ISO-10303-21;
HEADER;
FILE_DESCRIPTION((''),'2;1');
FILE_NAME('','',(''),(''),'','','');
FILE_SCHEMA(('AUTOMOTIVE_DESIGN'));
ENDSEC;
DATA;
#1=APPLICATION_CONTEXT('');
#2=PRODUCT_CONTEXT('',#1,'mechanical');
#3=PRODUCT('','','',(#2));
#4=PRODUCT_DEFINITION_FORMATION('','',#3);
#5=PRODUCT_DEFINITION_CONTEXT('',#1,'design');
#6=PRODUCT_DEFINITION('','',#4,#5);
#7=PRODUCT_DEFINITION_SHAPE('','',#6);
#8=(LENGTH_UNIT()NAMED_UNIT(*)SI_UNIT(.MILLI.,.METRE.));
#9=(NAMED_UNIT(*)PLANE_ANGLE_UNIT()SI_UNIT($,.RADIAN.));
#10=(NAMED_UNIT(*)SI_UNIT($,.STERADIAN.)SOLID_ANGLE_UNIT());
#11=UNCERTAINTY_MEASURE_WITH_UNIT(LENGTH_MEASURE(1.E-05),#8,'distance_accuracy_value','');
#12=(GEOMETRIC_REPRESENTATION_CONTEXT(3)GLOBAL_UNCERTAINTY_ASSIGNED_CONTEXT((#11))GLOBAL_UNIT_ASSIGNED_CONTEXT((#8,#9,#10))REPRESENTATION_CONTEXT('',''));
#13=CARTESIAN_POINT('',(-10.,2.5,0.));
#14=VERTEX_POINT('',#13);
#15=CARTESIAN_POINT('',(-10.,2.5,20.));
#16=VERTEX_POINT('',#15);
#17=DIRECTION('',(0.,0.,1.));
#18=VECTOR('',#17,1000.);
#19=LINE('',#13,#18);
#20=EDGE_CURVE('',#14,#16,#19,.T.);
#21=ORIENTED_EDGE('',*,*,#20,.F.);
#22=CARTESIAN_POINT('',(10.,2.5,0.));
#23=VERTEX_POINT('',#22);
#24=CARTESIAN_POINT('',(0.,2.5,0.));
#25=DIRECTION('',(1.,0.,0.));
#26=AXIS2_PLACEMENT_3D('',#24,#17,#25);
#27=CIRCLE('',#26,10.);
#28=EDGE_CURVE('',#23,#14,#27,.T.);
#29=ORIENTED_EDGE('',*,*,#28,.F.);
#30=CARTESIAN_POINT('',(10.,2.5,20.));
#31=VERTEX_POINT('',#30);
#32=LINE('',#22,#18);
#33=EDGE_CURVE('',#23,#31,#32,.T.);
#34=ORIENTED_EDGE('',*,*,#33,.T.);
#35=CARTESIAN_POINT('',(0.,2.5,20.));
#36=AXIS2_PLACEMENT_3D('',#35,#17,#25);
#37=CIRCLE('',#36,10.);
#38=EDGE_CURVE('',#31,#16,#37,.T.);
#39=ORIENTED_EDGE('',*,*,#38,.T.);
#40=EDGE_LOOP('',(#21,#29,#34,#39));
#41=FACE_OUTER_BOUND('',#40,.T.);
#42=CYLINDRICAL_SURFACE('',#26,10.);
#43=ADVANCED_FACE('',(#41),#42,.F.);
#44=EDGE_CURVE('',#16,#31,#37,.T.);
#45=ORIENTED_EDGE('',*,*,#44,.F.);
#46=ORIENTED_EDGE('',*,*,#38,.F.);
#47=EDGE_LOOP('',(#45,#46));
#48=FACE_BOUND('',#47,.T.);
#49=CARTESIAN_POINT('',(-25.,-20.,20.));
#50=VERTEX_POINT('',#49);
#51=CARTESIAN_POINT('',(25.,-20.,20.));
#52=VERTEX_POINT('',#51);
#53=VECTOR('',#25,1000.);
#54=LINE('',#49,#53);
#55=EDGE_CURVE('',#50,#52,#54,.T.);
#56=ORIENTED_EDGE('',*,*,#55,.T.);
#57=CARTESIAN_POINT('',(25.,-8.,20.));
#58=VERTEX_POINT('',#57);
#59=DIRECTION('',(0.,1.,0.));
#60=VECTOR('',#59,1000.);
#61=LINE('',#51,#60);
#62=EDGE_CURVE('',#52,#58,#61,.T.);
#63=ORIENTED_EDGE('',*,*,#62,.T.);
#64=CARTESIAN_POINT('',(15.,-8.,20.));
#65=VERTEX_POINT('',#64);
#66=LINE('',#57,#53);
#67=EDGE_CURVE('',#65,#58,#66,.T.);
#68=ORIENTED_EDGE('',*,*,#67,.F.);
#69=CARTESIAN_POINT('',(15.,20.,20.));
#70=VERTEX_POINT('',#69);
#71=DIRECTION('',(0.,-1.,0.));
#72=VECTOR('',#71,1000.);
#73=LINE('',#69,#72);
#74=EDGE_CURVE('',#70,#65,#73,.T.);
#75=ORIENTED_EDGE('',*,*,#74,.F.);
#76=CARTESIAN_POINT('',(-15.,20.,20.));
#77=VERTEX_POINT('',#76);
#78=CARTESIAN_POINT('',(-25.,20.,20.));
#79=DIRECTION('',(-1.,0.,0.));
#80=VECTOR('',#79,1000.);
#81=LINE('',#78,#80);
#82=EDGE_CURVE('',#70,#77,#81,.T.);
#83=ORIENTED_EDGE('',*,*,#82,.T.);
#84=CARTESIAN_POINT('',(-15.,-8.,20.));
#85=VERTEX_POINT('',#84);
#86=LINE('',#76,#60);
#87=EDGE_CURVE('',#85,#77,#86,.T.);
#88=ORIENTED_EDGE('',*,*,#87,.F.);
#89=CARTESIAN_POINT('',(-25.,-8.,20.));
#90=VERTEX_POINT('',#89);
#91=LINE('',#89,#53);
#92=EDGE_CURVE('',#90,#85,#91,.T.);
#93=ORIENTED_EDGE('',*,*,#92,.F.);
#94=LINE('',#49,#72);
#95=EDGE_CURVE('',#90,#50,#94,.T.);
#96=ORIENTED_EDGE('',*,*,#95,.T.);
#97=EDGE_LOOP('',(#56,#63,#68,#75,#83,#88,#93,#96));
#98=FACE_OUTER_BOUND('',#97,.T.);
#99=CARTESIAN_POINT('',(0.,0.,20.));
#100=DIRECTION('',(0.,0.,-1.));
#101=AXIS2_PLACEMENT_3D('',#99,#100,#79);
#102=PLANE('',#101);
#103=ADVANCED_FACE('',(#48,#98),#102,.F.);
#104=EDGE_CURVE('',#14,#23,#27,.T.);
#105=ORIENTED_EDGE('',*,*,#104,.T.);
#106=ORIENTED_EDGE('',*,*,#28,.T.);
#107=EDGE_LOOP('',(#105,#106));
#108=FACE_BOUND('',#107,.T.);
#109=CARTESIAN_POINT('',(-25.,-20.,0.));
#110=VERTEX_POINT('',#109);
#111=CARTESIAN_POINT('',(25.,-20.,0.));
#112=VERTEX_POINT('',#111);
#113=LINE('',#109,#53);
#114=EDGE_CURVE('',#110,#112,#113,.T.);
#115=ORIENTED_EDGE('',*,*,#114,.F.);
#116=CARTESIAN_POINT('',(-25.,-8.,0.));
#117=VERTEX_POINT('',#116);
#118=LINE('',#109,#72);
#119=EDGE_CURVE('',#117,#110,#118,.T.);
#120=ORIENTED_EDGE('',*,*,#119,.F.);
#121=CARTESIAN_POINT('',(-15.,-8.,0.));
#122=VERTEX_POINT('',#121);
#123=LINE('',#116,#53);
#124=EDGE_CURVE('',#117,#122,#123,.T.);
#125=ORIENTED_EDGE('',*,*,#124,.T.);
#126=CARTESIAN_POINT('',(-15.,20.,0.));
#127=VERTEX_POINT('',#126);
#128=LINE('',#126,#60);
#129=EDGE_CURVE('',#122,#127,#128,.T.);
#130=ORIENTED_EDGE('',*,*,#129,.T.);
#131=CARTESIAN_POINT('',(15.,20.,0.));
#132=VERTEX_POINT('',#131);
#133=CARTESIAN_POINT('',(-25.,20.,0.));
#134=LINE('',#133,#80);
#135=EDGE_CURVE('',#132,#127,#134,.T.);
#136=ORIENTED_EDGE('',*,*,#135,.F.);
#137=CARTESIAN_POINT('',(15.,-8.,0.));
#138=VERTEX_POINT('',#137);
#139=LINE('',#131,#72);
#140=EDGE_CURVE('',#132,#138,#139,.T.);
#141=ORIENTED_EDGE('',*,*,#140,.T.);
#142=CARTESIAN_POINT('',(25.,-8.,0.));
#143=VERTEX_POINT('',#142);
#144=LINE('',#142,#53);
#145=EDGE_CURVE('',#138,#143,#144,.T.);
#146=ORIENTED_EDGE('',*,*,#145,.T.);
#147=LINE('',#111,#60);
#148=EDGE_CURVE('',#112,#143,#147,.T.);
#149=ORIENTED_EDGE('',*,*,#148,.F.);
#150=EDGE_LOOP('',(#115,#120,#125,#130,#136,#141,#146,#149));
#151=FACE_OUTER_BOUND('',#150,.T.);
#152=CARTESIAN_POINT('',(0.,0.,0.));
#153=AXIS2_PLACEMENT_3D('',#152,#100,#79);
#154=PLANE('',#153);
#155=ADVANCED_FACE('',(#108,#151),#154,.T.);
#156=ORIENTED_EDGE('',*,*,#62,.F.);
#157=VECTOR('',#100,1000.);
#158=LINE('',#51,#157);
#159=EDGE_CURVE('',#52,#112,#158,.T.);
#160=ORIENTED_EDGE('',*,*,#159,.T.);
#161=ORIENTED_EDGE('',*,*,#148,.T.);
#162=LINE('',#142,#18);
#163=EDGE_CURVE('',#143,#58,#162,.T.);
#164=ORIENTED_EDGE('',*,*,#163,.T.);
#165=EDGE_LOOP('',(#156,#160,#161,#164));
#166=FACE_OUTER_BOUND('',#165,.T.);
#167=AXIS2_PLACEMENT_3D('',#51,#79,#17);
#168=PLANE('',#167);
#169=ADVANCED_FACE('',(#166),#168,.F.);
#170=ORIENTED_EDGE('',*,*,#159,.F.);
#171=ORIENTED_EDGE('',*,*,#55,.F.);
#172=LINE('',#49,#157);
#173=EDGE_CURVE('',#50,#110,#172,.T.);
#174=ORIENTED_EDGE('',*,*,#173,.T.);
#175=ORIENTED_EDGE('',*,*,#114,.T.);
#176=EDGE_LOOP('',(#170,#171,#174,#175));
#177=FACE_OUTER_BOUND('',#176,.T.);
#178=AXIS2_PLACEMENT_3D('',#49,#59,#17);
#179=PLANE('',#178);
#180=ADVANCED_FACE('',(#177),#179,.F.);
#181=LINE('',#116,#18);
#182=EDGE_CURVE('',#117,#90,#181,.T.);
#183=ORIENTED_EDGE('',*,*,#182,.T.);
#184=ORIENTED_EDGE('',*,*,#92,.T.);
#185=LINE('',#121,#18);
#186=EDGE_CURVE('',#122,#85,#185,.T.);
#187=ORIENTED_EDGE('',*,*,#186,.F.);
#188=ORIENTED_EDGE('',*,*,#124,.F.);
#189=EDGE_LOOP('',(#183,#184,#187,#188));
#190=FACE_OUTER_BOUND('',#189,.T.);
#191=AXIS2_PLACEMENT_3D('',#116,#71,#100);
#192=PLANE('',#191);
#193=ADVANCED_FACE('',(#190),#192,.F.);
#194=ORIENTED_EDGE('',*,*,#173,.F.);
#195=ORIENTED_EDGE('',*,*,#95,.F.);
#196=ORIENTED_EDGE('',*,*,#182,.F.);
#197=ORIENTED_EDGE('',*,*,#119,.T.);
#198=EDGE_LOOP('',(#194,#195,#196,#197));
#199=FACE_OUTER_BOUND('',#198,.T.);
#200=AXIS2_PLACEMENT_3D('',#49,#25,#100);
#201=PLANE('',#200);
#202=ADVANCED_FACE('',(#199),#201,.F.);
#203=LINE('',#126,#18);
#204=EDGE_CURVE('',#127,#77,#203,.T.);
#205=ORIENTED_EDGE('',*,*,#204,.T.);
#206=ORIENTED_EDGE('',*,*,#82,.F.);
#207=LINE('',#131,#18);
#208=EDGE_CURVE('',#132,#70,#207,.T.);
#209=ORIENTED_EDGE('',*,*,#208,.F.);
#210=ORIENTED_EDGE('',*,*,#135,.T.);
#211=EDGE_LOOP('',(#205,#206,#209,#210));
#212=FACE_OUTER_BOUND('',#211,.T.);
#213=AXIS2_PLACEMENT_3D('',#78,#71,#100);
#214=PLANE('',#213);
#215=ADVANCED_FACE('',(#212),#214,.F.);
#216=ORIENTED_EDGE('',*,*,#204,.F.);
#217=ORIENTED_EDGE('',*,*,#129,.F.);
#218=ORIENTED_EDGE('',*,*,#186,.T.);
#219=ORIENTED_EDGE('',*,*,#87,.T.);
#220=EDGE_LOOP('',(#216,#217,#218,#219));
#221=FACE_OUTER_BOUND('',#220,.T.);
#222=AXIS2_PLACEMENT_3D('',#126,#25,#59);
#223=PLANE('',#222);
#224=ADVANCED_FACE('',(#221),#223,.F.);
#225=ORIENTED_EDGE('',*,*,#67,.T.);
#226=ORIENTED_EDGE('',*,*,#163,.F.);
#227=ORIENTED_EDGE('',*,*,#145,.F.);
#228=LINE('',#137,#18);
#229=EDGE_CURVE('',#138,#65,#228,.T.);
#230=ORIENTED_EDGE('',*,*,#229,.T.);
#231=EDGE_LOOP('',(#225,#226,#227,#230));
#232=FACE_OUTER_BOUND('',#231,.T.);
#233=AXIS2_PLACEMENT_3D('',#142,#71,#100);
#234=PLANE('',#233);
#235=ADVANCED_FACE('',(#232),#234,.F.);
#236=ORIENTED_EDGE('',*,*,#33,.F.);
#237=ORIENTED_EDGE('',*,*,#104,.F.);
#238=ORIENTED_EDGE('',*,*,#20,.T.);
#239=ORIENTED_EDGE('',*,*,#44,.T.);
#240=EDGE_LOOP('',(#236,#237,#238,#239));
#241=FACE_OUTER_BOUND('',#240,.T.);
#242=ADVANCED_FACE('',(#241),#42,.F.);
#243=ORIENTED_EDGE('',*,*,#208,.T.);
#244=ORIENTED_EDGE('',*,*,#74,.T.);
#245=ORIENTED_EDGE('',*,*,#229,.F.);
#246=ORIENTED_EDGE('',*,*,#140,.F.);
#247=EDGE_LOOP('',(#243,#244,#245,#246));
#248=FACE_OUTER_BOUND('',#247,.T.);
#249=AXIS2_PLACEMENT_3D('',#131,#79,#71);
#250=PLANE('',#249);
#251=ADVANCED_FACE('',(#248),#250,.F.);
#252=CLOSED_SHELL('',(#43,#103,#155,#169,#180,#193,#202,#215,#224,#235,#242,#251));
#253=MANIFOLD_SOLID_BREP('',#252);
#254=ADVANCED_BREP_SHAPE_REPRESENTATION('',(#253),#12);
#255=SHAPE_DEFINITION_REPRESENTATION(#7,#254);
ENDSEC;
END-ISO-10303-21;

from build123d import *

# Parameters (mm, degrees)
SKETCH_1_W          = 50
SKETCH_1_H          = 40
EXTRUDE_1_DEPTH     = 20
SKETCH_2_R          = 10
CUT_EXTRUDE_1_DEPTH = 38.749172176
SKETCH_3_W          = 10
SKETCH_3_H          = 28
CUT_EXTRUDE_2_DEPTH = 38.749172176


with BuildPart() as part:
    # 草图1 → 凸台-拉伸1 (new body)
    with BuildSketch(Plane.XY):
        Rectangle(SKETCH_1_W, SKETCH_1_H)
    extrude(amount=EXTRUDE_1_DEPTH)

    # 草图2 → 切除-拉伸1 (cut, through all)
    with BuildSketch(Plane.XY.offset(20)):
        with Locations((0, 2.5)):
            Circle(SKETCH_2_R)
    extrude(amount=-CUT_EXTRUDE_1_DEPTH, mode=Mode.SUBTRACT)

    # 草图3 → 切除-拉伸2 (cut, through all)
    with BuildSketch(Plane.XY.offset(20)):
        with Locations((-20, 6)):
            Rectangle(SKETCH_3_W, SKETCH_3_H)
        with Locations((20, 6)):
            Rectangle(SKETCH_3_W, SKETCH_3_H)
    extrude(amount=-CUT_EXTRUDE_2_DEPTH, mode=Mode.SUBTRACT)


solid = part.part
